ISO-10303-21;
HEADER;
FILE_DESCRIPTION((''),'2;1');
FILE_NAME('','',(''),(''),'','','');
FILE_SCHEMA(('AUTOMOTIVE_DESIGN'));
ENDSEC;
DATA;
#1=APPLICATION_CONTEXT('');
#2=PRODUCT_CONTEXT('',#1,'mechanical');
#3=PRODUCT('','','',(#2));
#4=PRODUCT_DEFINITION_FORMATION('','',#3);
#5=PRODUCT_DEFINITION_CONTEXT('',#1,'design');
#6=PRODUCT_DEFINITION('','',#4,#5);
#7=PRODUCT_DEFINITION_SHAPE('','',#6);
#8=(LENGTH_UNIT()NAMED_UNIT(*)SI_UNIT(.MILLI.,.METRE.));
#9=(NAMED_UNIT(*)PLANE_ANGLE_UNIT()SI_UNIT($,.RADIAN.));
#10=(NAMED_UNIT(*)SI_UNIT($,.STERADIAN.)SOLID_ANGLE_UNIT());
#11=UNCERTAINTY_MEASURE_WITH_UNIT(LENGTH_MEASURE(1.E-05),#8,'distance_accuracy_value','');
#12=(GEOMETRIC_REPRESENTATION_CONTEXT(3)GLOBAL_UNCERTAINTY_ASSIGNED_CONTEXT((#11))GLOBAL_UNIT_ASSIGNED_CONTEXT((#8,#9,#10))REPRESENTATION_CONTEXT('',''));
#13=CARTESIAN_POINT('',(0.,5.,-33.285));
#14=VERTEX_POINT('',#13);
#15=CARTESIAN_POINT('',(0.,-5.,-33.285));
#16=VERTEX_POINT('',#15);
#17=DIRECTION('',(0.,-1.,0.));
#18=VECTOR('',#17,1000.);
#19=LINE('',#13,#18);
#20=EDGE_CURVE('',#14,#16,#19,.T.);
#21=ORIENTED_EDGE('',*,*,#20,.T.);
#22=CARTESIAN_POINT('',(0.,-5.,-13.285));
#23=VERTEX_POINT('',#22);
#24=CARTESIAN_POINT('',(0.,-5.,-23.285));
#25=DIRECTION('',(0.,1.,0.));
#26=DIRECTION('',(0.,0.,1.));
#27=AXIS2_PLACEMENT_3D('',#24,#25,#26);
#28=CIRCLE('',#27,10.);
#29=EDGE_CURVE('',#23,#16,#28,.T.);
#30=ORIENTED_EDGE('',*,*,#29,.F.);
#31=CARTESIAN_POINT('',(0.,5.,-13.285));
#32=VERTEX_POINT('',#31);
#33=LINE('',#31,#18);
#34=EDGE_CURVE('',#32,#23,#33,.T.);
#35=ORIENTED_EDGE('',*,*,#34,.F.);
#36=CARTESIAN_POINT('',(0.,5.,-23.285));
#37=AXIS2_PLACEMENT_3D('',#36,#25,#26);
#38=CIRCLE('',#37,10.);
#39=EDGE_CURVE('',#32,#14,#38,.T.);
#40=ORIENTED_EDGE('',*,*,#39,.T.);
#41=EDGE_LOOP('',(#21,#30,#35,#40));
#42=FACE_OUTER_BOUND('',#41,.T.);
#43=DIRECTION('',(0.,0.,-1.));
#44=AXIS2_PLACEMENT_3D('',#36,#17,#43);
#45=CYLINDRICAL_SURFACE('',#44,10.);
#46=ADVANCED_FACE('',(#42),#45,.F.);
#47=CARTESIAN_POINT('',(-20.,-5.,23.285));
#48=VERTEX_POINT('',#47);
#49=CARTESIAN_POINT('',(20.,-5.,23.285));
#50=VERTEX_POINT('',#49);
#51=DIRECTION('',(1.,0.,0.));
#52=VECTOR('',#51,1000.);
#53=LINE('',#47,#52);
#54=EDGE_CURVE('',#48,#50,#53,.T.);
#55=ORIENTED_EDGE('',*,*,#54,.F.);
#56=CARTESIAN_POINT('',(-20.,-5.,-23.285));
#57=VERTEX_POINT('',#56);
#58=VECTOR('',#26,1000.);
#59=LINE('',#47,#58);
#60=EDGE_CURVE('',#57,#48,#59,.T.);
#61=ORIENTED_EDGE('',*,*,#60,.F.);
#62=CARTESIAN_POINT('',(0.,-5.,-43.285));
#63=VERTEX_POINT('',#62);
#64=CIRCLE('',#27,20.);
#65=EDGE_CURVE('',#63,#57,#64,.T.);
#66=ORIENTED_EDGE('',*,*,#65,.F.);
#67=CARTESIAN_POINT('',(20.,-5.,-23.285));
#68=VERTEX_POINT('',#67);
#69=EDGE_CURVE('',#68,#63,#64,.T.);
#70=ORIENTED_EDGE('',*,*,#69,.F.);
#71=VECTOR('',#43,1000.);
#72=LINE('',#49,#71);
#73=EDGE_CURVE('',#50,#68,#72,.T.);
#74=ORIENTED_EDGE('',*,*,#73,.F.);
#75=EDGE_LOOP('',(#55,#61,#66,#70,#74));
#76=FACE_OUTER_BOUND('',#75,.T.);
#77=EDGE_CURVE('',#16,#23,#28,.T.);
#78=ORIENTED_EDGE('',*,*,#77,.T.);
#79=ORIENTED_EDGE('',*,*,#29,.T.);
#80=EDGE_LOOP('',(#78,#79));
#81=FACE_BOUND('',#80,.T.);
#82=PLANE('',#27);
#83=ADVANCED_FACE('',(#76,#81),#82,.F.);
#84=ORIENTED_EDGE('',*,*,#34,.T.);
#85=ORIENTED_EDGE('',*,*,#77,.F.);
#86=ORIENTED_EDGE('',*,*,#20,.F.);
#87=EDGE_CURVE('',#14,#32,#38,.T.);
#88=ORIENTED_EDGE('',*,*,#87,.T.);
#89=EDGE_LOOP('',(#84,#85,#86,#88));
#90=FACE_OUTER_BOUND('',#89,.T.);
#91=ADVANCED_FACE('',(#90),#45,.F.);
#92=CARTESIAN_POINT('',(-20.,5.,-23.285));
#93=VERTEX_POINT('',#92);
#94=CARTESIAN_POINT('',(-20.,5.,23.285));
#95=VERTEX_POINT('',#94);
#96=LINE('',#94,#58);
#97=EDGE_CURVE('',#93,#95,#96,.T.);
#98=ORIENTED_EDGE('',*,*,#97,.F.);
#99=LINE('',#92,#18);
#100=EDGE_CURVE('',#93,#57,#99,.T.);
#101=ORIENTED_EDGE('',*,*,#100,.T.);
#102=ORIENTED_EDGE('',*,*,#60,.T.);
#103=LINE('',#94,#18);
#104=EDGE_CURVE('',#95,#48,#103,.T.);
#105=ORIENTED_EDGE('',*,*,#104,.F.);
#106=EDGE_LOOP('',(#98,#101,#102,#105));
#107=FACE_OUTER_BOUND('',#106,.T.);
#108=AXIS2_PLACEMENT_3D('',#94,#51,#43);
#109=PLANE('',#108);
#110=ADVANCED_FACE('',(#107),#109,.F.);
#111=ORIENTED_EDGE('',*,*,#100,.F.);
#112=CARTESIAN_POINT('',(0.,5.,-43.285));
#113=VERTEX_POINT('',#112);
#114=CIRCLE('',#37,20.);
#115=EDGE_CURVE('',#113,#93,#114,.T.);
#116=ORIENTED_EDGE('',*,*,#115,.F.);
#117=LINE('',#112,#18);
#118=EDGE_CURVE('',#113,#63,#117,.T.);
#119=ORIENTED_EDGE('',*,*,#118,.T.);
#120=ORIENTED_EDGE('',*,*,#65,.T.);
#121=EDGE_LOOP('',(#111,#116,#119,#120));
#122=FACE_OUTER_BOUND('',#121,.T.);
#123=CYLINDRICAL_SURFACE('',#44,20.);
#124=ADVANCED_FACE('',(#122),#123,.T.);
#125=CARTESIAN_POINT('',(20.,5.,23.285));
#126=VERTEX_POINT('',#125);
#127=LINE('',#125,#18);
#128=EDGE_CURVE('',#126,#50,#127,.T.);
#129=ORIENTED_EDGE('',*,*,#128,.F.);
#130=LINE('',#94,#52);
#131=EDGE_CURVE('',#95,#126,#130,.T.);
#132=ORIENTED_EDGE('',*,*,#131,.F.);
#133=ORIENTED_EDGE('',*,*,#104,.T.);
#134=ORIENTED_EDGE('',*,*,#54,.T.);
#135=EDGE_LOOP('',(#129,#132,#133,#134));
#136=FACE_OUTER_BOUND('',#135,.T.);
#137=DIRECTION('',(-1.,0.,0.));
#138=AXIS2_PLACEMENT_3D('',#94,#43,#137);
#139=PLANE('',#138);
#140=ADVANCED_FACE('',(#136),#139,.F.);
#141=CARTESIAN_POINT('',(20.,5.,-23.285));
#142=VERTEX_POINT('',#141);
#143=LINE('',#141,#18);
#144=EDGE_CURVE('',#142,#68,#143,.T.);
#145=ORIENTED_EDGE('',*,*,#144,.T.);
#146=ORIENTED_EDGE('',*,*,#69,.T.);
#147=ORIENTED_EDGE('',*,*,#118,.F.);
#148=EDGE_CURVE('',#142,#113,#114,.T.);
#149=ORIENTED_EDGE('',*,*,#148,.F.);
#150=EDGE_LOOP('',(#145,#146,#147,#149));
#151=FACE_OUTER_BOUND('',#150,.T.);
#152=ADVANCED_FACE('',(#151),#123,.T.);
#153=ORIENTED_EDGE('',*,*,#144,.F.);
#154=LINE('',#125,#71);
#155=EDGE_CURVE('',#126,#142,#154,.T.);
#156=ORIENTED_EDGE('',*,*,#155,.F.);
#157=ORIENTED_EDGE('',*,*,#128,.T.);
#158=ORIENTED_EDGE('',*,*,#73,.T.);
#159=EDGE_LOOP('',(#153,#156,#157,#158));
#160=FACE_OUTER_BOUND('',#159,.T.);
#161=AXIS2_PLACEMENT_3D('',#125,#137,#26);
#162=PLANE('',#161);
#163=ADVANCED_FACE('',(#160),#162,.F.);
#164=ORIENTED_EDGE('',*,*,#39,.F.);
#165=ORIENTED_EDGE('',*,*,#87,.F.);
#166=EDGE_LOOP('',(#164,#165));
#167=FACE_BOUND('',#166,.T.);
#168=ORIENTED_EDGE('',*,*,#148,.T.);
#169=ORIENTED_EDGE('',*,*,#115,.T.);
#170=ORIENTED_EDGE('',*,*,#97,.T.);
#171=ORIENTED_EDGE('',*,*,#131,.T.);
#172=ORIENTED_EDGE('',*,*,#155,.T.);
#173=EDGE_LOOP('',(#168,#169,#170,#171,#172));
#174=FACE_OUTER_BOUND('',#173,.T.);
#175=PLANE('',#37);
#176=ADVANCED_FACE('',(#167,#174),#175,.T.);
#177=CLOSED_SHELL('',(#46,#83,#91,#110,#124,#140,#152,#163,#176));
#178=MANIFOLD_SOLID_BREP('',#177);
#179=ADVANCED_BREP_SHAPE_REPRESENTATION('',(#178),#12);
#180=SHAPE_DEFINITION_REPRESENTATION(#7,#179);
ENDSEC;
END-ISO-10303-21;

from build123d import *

# Parameters (mm, degrees)
SKETCH_1_R      = 10
EXTRUDE_1_DEPTH = 5


with BuildPart() as part:
    # 草图1 → 凸台-拉伸1 (new, symmetric)
    with BuildSketch(Plane(origin=(0, 0, 0), x_dir=(1, 0, 0), z_dir=(0, 1, 0))):
        with BuildLine():
            Line((-20, -23.285), (20, -23.285))
            Line((20, -23.285), (20, 23.285))
            ThreePointArc((20, 23.285), (0, 43.285), (-20, 23.285))
            Line((-20, 23.285), (-20, -23.285))
        make_face()
        with Locations(Location((0, 23.285, 0), (0, 0, 270))):
            Circle(SKETCH_1_R, mode=Mode.SUBTRACT)
    extrude(amount=EXTRUDE_1_DEPTH, both=True)


solid = part.part
